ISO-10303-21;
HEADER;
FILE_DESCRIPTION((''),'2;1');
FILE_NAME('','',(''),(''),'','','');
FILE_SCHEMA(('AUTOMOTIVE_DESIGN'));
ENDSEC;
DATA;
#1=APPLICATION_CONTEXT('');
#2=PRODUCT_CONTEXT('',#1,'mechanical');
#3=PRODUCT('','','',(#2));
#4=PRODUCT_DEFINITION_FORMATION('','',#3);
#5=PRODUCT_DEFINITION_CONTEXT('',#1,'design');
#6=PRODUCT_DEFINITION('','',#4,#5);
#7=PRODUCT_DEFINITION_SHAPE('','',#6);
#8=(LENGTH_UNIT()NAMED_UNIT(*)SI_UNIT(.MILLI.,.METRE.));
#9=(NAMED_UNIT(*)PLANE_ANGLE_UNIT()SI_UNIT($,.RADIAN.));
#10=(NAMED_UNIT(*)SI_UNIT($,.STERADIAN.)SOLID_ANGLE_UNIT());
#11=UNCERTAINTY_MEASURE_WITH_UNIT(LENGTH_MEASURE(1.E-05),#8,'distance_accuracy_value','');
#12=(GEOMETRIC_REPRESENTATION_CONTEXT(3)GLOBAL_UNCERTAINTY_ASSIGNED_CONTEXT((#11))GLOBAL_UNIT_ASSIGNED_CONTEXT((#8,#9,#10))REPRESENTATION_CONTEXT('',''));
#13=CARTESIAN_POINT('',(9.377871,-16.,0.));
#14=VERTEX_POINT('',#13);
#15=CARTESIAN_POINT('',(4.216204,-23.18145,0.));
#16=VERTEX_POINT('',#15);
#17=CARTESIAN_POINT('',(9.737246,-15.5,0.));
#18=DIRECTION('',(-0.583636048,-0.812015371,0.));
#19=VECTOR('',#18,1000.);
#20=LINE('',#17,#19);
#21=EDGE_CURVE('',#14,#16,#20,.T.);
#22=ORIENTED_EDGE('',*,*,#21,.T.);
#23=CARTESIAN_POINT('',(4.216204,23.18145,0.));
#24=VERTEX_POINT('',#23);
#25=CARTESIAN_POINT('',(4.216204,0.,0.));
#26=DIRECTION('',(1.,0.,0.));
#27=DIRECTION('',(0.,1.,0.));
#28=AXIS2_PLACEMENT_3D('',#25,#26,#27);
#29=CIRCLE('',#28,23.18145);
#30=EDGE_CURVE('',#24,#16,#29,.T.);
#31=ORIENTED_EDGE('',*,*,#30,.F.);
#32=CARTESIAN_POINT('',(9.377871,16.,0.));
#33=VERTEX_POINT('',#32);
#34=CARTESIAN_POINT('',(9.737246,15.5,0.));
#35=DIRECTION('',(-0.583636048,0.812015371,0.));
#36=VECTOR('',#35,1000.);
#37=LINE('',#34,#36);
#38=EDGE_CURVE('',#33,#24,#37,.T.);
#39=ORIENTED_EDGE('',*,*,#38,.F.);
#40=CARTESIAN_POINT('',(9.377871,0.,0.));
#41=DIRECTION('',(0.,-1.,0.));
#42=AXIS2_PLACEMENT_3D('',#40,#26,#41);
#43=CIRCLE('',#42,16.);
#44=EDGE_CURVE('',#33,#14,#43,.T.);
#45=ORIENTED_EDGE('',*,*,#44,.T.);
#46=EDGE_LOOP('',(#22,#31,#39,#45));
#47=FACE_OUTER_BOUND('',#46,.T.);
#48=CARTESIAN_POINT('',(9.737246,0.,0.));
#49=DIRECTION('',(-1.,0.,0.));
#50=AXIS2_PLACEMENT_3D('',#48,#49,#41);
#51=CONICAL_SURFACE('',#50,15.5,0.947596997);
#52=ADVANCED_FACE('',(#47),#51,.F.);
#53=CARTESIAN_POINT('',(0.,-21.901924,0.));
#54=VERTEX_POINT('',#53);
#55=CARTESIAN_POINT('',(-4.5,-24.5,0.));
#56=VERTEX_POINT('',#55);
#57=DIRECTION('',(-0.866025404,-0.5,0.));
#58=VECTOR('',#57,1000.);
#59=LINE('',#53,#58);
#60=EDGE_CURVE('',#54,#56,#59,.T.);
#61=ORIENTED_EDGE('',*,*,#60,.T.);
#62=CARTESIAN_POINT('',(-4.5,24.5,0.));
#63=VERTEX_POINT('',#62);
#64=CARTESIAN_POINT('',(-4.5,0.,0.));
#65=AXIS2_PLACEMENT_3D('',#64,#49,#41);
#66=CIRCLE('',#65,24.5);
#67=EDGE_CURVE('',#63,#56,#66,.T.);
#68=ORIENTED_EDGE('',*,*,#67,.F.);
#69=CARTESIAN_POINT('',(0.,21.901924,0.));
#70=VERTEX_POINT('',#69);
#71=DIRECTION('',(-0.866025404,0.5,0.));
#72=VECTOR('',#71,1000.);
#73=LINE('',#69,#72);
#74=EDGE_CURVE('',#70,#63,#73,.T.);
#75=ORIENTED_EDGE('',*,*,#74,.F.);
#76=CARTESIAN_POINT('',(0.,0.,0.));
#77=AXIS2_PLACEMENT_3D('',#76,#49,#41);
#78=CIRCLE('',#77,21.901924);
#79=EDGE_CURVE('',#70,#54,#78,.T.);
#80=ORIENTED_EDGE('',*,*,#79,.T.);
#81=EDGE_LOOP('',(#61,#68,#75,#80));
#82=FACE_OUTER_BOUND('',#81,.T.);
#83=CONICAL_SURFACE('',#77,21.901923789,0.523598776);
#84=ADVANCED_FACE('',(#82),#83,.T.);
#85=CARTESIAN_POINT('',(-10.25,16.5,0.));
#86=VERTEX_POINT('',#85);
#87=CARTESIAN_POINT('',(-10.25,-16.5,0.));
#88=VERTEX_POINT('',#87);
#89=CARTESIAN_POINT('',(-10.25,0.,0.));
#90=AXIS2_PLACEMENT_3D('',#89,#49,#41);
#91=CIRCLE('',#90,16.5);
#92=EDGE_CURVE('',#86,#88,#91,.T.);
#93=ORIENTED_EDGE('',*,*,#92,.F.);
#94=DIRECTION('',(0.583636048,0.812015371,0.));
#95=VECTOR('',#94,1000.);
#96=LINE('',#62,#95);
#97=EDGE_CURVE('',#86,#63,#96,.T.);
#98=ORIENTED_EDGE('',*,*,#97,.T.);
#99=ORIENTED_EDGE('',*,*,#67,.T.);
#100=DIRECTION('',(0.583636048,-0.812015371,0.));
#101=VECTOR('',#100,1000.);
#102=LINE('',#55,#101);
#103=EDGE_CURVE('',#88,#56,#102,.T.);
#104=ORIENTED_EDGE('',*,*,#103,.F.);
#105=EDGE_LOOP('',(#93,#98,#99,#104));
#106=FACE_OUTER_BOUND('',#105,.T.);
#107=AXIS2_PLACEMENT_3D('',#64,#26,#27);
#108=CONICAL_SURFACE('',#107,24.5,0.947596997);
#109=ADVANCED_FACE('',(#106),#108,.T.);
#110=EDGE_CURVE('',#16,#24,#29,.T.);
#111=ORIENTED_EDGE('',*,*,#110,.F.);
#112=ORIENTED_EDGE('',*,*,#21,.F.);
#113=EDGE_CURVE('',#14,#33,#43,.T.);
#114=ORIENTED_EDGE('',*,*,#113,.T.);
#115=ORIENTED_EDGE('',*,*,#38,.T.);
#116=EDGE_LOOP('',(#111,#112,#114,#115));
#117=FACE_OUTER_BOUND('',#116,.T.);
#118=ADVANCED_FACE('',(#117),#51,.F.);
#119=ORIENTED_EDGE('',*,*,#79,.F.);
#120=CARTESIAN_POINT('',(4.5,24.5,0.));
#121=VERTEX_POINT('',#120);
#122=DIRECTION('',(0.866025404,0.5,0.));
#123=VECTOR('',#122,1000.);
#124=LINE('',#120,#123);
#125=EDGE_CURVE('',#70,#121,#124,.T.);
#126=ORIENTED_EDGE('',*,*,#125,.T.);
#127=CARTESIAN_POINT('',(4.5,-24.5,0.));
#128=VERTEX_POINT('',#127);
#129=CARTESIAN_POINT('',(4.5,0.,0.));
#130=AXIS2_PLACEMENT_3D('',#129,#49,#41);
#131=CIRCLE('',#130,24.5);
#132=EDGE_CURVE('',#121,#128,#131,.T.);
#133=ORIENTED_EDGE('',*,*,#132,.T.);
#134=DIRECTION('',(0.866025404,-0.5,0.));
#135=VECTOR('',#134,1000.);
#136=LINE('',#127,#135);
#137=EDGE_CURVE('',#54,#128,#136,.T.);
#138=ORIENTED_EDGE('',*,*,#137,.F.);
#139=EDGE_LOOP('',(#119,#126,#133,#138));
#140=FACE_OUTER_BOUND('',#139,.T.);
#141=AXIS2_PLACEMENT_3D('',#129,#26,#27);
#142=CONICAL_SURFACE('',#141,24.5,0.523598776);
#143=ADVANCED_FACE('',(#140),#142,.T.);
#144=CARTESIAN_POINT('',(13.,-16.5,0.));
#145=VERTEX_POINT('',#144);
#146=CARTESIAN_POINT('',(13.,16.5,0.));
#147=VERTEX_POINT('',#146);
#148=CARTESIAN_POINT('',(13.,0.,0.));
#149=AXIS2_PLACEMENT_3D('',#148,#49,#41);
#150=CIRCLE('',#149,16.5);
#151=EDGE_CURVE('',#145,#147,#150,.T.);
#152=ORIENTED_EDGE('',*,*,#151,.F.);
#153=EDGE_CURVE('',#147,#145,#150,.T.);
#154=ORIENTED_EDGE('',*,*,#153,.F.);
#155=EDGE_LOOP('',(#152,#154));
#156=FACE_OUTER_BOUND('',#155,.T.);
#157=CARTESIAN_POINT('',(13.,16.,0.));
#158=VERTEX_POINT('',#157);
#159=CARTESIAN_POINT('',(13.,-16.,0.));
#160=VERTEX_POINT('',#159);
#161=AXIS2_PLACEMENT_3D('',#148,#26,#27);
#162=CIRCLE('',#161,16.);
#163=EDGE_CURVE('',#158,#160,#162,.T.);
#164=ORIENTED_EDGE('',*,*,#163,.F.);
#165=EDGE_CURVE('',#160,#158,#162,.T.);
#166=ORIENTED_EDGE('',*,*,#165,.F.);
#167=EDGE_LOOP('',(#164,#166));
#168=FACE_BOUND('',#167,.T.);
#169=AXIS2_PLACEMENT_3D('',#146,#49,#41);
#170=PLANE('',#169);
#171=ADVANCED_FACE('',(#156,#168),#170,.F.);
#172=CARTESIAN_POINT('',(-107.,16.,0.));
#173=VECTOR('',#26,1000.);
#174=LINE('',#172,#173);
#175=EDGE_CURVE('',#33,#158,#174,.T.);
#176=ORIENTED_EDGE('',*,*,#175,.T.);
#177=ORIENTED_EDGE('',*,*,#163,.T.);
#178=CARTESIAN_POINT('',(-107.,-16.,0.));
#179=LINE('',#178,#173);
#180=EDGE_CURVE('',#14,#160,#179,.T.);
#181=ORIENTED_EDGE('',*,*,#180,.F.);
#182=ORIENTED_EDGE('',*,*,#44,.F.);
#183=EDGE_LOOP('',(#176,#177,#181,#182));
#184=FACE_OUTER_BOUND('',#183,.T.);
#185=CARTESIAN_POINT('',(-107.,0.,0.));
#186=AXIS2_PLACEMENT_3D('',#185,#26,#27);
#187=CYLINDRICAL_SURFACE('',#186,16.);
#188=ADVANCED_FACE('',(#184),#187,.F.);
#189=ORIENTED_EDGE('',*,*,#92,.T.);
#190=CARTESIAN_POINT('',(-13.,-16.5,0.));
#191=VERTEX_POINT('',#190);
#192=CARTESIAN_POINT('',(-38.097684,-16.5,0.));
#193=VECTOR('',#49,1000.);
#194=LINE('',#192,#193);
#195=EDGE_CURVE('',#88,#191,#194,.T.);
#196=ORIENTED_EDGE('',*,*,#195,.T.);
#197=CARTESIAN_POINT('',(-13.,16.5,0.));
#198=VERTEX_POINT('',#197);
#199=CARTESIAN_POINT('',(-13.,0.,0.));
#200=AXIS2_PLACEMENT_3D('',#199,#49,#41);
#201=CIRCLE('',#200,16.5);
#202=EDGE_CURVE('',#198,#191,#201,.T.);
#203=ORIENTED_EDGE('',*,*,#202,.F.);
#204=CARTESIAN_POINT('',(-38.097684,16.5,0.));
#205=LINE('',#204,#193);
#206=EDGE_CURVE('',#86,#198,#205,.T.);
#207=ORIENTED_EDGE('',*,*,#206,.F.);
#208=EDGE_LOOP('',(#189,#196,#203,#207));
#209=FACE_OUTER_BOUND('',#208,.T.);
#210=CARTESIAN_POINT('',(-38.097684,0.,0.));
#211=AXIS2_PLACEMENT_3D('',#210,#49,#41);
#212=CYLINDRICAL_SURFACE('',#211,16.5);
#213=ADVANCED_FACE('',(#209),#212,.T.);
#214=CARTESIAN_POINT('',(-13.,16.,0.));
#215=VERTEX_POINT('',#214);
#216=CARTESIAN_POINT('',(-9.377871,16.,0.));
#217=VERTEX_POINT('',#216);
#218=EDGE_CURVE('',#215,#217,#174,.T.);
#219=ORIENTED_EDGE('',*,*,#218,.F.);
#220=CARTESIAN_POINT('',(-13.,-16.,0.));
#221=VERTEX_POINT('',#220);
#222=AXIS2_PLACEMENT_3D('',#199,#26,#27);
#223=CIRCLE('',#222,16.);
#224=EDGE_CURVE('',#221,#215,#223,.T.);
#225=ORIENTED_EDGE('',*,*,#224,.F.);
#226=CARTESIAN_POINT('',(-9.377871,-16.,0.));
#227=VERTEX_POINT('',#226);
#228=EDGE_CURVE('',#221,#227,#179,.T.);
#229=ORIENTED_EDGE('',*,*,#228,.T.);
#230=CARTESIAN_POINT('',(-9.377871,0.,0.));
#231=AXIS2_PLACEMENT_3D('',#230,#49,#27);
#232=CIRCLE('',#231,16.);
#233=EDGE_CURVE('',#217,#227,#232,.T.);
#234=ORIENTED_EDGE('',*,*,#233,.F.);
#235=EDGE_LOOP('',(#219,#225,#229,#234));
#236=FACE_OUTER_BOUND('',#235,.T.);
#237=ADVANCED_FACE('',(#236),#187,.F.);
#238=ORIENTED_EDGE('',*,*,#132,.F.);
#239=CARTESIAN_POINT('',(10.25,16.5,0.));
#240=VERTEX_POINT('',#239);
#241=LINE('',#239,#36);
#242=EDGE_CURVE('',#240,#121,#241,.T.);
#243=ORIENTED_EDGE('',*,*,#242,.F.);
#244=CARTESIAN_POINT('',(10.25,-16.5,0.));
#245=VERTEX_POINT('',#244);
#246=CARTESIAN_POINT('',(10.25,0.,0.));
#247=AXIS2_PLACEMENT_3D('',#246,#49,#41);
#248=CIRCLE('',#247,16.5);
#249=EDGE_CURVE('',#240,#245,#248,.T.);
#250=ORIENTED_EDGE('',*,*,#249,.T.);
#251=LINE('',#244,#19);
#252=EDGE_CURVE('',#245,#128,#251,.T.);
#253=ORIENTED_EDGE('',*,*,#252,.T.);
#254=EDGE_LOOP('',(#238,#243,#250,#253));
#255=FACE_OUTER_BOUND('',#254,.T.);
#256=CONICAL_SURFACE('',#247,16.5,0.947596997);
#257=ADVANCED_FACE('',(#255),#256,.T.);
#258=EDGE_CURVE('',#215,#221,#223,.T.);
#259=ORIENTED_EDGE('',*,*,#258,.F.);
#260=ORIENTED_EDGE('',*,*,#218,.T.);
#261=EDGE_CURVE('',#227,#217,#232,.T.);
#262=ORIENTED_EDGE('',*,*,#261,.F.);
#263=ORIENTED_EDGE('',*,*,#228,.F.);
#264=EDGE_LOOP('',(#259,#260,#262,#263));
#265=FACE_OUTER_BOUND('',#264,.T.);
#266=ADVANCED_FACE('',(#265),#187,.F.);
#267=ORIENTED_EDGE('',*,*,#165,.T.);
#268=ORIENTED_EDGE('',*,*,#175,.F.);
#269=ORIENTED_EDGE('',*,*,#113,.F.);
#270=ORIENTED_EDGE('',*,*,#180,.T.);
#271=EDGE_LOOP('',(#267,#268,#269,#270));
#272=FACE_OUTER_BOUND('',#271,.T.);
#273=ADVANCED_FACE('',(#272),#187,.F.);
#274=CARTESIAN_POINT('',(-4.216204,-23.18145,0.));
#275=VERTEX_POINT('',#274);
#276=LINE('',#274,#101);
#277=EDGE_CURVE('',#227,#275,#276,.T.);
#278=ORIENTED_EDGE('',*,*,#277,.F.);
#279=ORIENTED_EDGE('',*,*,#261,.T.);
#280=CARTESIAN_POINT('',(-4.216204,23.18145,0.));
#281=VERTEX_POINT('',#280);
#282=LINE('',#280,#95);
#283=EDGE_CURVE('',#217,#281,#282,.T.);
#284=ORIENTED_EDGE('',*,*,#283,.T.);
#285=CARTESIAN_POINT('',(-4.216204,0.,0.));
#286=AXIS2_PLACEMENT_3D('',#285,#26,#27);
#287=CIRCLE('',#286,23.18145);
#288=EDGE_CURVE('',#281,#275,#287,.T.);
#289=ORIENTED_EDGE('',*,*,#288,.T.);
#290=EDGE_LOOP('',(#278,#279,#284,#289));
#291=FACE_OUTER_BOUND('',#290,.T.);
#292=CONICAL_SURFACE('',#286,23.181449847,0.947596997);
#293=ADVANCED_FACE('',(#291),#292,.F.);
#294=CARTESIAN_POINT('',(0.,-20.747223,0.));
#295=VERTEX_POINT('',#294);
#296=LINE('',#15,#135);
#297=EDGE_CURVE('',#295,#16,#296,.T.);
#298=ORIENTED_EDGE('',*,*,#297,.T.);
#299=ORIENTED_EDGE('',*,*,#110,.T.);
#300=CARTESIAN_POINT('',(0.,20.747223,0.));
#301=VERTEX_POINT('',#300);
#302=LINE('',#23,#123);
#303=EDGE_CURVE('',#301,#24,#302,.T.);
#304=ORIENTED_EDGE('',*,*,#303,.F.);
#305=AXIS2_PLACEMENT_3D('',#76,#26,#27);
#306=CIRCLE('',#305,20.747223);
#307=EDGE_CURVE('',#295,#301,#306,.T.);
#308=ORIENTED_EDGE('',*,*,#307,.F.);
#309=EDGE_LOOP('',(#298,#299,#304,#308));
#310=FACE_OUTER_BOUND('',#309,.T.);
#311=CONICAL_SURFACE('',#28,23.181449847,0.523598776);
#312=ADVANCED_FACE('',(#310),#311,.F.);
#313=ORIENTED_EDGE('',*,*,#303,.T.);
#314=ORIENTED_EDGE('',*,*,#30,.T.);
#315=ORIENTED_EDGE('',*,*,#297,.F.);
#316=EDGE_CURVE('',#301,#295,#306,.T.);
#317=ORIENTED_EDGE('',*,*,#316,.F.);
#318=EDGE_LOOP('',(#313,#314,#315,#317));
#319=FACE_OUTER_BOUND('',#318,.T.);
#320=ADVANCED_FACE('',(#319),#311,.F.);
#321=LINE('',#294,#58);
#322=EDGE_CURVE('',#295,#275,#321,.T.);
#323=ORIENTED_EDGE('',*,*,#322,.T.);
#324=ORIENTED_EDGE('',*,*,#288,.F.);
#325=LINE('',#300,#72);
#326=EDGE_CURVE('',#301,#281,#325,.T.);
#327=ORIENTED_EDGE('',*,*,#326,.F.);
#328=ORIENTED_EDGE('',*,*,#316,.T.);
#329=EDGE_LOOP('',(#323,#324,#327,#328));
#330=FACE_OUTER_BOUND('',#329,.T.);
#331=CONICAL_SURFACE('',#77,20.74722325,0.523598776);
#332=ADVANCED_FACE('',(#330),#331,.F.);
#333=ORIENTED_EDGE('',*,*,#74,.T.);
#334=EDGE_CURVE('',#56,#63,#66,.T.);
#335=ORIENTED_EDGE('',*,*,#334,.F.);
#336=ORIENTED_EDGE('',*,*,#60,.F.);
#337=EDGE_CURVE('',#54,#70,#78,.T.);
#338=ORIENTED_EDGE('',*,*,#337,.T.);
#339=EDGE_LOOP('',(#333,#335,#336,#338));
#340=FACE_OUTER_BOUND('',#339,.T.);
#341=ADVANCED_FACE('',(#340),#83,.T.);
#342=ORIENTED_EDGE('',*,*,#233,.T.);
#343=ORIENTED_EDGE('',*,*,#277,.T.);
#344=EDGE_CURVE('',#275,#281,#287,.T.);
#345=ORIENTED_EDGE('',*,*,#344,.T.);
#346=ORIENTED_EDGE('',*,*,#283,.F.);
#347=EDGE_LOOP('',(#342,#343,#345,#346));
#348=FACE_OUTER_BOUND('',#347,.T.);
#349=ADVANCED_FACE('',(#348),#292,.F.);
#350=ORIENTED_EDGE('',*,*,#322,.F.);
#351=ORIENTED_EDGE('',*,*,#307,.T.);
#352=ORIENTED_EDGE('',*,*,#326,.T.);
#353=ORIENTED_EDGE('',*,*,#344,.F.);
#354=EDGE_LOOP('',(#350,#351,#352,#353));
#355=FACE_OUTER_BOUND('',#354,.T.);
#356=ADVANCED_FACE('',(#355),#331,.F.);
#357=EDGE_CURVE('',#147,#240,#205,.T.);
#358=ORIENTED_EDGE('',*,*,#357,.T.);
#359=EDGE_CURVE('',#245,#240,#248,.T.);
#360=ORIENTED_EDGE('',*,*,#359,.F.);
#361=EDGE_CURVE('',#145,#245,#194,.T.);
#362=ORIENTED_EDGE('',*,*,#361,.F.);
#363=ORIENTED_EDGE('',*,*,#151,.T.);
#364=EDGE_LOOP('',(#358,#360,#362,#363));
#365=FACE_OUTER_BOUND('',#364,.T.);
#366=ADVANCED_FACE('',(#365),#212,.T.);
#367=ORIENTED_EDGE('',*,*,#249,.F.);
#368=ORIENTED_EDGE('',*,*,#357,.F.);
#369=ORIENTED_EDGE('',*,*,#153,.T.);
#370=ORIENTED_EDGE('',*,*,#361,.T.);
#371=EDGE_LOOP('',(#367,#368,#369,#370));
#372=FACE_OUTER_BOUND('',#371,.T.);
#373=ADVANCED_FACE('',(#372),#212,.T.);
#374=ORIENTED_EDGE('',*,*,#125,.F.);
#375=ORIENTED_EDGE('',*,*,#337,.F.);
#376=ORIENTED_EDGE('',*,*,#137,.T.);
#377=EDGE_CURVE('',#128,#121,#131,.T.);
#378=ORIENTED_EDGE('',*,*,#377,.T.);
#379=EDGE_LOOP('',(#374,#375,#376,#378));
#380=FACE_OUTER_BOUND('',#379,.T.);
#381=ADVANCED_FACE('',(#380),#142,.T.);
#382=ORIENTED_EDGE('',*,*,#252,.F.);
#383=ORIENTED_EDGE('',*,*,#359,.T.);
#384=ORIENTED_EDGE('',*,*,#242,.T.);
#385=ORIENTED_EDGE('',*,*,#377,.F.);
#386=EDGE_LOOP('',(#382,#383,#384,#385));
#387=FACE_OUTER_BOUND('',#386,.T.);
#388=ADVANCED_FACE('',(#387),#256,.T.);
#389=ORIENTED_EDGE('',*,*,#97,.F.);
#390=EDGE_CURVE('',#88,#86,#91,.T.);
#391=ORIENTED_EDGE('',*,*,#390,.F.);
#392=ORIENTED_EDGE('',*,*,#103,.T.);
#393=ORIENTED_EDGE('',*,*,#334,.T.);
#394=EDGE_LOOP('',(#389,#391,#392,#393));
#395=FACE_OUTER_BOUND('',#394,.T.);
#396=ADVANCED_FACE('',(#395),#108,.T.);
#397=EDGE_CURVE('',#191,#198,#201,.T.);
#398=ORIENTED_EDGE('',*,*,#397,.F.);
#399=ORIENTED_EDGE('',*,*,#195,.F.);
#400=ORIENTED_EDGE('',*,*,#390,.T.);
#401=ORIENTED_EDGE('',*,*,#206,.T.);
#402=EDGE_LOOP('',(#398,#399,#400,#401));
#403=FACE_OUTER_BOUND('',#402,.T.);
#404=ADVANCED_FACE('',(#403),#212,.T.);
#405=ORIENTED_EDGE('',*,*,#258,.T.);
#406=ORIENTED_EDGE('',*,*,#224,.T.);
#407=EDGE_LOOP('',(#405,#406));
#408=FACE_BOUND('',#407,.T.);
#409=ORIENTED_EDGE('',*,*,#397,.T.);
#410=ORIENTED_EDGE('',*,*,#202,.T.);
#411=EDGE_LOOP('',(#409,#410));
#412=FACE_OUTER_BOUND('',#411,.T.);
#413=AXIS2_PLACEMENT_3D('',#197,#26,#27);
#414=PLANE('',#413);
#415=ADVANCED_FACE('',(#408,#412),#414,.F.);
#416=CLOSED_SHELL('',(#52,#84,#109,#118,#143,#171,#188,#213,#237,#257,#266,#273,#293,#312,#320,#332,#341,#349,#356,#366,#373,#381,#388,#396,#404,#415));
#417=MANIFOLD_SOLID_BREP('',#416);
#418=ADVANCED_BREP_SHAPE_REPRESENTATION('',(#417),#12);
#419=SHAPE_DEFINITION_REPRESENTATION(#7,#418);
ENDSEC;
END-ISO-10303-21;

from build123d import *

# Parameters (mm, degrees)
SKETCH4_R          = 16
CUT_EXTRUDE2_DEPTH = 120


with BuildPart() as part:
    # Sketch1 → Revolve1 (revolve)
    with BuildSketch(Plane.XY, mode=Mode.PRIVATE) as revolve1_sk:
        Polygon((0, 21.901923789), (4.5, 24.5), (10.25, 16.5), (13, 16.5), (13, 0), (-13, 0), (-13, 16.5), (-10.25, 16.5), (-4.5, 24.5), align=None)
    revolve(revolve1_sk.sketch.rotate(Axis((-38.0976844, 0, 0), (1, 0, 0)), 180), axis=Axis((-38.0976844, 0, 0), (1, 0, 0)))

    # Sketch3 → Cut-Revolve1 (revolve, cut)
    with BuildSketch(Plane.XY):
        Polygon((4.216204142, 23.181449847), (0, 20.74722325), (-4.216204142, 23.181449847), (-9.737246219, 15.5), (-12, 15.5), (-12, 1), (-12, 0), (12, 0), (12, 1), (12, 15.5), (9.737246219, 15.5), align=None)
    revolve(axis=Axis((12, 0, 0), (-1, 0, 0)), mode=Mode.SUBTRACT)

    # Sketch4 → Cut-Extrude2 (cut)
    with BuildSketch(Plane(origin=(13, 0, 0), x_dir=(0, 0, -1), z_dir=(1, 0, 0))):
        with Locations(Location((0, 0, 0), (0, 0, 90))):
            Circle(SKETCH4_R)
    extrude(amount=-CUT_EXTRUDE2_DEPTH, mode=Mode.SUBTRACT)


solid = part.part
